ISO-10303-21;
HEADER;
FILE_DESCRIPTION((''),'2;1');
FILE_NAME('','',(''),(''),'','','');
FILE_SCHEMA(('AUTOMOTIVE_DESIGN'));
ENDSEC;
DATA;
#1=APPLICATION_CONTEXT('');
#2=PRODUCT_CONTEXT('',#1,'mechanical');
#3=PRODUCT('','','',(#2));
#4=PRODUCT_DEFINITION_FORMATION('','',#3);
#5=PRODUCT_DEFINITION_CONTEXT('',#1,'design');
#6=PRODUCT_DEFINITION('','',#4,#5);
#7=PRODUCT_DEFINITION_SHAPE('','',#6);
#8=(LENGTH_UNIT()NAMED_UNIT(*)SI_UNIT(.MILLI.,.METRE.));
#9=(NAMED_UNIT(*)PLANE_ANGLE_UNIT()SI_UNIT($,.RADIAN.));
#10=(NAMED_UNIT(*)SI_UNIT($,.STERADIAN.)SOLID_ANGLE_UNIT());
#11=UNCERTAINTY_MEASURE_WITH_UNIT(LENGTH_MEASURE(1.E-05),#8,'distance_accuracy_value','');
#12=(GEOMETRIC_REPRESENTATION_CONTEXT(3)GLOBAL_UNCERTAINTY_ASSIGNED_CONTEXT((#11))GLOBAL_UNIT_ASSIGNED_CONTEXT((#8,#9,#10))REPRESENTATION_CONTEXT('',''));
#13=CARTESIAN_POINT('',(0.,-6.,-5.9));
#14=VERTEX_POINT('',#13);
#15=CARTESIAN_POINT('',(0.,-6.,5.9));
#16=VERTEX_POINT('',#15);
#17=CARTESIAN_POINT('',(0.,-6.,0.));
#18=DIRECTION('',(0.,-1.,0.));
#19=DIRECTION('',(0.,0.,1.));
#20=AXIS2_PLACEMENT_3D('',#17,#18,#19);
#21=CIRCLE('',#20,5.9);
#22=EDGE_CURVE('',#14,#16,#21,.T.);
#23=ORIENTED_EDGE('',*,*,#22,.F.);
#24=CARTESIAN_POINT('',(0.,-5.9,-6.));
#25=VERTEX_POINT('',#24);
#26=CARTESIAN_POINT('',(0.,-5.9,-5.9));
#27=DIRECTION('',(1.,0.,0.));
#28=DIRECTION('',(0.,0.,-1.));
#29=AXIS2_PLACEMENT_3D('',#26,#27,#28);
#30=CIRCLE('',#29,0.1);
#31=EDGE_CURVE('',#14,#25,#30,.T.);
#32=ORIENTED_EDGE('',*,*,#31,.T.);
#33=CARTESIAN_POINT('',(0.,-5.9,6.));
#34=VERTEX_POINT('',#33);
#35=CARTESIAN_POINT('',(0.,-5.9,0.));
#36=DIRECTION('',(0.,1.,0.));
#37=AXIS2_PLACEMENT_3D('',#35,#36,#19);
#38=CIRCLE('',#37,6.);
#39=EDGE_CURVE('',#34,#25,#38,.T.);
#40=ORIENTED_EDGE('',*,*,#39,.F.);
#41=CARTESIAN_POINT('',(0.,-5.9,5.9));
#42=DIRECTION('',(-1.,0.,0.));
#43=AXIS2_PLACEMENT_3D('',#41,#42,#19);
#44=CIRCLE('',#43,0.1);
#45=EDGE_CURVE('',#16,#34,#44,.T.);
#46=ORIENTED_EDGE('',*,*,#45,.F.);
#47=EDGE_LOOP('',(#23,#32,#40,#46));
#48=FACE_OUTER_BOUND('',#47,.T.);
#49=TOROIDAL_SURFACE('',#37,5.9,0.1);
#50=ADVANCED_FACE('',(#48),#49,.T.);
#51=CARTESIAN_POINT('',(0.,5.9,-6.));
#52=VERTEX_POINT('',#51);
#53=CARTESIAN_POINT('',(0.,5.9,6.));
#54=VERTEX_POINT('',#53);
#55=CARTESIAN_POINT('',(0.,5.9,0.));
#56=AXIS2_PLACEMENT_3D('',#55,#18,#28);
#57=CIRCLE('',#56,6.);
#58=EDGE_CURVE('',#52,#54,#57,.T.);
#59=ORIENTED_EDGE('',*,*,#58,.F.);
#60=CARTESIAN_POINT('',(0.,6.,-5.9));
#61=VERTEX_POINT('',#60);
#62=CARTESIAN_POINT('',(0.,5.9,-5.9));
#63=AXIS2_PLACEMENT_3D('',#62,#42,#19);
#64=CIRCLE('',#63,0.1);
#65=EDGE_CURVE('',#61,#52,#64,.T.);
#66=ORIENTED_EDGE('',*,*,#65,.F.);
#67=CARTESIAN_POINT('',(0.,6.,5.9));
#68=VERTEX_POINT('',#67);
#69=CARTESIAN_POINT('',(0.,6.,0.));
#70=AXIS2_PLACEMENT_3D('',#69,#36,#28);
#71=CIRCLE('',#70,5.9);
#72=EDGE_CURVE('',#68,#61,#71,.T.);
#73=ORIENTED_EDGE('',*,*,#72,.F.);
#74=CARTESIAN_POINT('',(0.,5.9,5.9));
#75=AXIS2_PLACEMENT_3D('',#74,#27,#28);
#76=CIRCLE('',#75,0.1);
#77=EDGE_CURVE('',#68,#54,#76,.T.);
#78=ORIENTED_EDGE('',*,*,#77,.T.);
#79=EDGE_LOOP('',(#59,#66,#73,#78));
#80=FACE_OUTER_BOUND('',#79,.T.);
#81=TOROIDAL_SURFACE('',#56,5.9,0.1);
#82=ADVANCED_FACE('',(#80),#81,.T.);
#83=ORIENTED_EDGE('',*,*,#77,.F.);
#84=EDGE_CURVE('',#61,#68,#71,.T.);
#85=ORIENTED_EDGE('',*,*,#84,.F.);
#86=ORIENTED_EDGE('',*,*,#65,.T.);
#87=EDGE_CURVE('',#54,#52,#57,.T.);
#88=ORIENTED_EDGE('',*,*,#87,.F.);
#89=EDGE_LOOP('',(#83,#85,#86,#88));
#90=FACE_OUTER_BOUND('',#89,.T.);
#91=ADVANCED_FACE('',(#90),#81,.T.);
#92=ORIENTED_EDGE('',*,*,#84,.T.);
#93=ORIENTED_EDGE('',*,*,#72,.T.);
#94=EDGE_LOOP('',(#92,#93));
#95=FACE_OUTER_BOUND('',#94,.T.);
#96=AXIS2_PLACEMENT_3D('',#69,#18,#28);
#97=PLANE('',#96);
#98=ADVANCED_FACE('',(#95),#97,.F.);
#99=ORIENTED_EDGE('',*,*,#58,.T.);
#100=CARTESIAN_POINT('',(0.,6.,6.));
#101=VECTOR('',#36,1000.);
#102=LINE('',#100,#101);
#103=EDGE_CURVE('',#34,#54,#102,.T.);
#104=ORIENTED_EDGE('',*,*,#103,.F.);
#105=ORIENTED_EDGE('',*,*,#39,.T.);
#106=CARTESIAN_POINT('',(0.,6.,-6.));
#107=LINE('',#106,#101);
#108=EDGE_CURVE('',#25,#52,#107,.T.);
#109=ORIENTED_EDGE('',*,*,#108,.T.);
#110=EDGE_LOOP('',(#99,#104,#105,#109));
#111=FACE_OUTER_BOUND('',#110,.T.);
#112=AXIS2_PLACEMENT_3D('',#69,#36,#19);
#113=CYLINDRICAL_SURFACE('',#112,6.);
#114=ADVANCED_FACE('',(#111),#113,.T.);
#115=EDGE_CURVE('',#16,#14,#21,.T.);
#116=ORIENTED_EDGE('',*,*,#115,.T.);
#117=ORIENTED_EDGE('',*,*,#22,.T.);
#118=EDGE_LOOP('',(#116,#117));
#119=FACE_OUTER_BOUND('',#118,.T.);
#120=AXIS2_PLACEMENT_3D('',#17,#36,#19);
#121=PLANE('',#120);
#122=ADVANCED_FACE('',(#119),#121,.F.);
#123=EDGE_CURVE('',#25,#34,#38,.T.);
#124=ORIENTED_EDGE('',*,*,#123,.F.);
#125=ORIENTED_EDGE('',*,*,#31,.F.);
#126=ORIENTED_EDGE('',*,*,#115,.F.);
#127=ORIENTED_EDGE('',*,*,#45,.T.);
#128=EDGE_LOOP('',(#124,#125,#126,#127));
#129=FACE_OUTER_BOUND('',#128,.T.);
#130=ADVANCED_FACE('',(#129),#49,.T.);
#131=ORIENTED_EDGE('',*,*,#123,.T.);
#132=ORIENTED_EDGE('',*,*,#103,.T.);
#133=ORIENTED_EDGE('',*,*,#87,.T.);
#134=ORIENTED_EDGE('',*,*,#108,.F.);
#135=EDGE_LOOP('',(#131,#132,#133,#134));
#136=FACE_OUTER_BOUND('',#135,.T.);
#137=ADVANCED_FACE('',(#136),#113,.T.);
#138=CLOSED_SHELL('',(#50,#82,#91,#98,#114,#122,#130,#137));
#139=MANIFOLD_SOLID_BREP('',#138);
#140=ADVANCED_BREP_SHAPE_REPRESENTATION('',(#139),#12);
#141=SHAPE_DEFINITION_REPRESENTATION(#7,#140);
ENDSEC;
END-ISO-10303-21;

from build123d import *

# Parameters (mm, degrees)
SKETCH_1_W = 6
SKETCH_1_H = 12
FILLET_1_R = 0.1


with BuildPart() as part:
    # 草图1 → 旋转2 (revolve)
    with BuildSketch(Plane.XY, mode=Mode.PRIVATE) as revolve_2_sk:
        with Locations((3, 0)):
            Rectangle(SKETCH_1_W, SKETCH_1_H)
    revolve(revolve_2_sk.sketch.rotate(Axis((0, 6, 0), (0, -1, 0)), 90), axis=Axis((0, 6, 0), (0, -1, 0)))

    # 圆角1
    fillet_1_edges = [part.edges().sort_by_distance(p)[0] for p in [
        (0, -6, -6),
        (0, 6, -6),
    ]]
    fillet(fillet_1_edges, radius=FILLET_1_R)


solid = part.part
